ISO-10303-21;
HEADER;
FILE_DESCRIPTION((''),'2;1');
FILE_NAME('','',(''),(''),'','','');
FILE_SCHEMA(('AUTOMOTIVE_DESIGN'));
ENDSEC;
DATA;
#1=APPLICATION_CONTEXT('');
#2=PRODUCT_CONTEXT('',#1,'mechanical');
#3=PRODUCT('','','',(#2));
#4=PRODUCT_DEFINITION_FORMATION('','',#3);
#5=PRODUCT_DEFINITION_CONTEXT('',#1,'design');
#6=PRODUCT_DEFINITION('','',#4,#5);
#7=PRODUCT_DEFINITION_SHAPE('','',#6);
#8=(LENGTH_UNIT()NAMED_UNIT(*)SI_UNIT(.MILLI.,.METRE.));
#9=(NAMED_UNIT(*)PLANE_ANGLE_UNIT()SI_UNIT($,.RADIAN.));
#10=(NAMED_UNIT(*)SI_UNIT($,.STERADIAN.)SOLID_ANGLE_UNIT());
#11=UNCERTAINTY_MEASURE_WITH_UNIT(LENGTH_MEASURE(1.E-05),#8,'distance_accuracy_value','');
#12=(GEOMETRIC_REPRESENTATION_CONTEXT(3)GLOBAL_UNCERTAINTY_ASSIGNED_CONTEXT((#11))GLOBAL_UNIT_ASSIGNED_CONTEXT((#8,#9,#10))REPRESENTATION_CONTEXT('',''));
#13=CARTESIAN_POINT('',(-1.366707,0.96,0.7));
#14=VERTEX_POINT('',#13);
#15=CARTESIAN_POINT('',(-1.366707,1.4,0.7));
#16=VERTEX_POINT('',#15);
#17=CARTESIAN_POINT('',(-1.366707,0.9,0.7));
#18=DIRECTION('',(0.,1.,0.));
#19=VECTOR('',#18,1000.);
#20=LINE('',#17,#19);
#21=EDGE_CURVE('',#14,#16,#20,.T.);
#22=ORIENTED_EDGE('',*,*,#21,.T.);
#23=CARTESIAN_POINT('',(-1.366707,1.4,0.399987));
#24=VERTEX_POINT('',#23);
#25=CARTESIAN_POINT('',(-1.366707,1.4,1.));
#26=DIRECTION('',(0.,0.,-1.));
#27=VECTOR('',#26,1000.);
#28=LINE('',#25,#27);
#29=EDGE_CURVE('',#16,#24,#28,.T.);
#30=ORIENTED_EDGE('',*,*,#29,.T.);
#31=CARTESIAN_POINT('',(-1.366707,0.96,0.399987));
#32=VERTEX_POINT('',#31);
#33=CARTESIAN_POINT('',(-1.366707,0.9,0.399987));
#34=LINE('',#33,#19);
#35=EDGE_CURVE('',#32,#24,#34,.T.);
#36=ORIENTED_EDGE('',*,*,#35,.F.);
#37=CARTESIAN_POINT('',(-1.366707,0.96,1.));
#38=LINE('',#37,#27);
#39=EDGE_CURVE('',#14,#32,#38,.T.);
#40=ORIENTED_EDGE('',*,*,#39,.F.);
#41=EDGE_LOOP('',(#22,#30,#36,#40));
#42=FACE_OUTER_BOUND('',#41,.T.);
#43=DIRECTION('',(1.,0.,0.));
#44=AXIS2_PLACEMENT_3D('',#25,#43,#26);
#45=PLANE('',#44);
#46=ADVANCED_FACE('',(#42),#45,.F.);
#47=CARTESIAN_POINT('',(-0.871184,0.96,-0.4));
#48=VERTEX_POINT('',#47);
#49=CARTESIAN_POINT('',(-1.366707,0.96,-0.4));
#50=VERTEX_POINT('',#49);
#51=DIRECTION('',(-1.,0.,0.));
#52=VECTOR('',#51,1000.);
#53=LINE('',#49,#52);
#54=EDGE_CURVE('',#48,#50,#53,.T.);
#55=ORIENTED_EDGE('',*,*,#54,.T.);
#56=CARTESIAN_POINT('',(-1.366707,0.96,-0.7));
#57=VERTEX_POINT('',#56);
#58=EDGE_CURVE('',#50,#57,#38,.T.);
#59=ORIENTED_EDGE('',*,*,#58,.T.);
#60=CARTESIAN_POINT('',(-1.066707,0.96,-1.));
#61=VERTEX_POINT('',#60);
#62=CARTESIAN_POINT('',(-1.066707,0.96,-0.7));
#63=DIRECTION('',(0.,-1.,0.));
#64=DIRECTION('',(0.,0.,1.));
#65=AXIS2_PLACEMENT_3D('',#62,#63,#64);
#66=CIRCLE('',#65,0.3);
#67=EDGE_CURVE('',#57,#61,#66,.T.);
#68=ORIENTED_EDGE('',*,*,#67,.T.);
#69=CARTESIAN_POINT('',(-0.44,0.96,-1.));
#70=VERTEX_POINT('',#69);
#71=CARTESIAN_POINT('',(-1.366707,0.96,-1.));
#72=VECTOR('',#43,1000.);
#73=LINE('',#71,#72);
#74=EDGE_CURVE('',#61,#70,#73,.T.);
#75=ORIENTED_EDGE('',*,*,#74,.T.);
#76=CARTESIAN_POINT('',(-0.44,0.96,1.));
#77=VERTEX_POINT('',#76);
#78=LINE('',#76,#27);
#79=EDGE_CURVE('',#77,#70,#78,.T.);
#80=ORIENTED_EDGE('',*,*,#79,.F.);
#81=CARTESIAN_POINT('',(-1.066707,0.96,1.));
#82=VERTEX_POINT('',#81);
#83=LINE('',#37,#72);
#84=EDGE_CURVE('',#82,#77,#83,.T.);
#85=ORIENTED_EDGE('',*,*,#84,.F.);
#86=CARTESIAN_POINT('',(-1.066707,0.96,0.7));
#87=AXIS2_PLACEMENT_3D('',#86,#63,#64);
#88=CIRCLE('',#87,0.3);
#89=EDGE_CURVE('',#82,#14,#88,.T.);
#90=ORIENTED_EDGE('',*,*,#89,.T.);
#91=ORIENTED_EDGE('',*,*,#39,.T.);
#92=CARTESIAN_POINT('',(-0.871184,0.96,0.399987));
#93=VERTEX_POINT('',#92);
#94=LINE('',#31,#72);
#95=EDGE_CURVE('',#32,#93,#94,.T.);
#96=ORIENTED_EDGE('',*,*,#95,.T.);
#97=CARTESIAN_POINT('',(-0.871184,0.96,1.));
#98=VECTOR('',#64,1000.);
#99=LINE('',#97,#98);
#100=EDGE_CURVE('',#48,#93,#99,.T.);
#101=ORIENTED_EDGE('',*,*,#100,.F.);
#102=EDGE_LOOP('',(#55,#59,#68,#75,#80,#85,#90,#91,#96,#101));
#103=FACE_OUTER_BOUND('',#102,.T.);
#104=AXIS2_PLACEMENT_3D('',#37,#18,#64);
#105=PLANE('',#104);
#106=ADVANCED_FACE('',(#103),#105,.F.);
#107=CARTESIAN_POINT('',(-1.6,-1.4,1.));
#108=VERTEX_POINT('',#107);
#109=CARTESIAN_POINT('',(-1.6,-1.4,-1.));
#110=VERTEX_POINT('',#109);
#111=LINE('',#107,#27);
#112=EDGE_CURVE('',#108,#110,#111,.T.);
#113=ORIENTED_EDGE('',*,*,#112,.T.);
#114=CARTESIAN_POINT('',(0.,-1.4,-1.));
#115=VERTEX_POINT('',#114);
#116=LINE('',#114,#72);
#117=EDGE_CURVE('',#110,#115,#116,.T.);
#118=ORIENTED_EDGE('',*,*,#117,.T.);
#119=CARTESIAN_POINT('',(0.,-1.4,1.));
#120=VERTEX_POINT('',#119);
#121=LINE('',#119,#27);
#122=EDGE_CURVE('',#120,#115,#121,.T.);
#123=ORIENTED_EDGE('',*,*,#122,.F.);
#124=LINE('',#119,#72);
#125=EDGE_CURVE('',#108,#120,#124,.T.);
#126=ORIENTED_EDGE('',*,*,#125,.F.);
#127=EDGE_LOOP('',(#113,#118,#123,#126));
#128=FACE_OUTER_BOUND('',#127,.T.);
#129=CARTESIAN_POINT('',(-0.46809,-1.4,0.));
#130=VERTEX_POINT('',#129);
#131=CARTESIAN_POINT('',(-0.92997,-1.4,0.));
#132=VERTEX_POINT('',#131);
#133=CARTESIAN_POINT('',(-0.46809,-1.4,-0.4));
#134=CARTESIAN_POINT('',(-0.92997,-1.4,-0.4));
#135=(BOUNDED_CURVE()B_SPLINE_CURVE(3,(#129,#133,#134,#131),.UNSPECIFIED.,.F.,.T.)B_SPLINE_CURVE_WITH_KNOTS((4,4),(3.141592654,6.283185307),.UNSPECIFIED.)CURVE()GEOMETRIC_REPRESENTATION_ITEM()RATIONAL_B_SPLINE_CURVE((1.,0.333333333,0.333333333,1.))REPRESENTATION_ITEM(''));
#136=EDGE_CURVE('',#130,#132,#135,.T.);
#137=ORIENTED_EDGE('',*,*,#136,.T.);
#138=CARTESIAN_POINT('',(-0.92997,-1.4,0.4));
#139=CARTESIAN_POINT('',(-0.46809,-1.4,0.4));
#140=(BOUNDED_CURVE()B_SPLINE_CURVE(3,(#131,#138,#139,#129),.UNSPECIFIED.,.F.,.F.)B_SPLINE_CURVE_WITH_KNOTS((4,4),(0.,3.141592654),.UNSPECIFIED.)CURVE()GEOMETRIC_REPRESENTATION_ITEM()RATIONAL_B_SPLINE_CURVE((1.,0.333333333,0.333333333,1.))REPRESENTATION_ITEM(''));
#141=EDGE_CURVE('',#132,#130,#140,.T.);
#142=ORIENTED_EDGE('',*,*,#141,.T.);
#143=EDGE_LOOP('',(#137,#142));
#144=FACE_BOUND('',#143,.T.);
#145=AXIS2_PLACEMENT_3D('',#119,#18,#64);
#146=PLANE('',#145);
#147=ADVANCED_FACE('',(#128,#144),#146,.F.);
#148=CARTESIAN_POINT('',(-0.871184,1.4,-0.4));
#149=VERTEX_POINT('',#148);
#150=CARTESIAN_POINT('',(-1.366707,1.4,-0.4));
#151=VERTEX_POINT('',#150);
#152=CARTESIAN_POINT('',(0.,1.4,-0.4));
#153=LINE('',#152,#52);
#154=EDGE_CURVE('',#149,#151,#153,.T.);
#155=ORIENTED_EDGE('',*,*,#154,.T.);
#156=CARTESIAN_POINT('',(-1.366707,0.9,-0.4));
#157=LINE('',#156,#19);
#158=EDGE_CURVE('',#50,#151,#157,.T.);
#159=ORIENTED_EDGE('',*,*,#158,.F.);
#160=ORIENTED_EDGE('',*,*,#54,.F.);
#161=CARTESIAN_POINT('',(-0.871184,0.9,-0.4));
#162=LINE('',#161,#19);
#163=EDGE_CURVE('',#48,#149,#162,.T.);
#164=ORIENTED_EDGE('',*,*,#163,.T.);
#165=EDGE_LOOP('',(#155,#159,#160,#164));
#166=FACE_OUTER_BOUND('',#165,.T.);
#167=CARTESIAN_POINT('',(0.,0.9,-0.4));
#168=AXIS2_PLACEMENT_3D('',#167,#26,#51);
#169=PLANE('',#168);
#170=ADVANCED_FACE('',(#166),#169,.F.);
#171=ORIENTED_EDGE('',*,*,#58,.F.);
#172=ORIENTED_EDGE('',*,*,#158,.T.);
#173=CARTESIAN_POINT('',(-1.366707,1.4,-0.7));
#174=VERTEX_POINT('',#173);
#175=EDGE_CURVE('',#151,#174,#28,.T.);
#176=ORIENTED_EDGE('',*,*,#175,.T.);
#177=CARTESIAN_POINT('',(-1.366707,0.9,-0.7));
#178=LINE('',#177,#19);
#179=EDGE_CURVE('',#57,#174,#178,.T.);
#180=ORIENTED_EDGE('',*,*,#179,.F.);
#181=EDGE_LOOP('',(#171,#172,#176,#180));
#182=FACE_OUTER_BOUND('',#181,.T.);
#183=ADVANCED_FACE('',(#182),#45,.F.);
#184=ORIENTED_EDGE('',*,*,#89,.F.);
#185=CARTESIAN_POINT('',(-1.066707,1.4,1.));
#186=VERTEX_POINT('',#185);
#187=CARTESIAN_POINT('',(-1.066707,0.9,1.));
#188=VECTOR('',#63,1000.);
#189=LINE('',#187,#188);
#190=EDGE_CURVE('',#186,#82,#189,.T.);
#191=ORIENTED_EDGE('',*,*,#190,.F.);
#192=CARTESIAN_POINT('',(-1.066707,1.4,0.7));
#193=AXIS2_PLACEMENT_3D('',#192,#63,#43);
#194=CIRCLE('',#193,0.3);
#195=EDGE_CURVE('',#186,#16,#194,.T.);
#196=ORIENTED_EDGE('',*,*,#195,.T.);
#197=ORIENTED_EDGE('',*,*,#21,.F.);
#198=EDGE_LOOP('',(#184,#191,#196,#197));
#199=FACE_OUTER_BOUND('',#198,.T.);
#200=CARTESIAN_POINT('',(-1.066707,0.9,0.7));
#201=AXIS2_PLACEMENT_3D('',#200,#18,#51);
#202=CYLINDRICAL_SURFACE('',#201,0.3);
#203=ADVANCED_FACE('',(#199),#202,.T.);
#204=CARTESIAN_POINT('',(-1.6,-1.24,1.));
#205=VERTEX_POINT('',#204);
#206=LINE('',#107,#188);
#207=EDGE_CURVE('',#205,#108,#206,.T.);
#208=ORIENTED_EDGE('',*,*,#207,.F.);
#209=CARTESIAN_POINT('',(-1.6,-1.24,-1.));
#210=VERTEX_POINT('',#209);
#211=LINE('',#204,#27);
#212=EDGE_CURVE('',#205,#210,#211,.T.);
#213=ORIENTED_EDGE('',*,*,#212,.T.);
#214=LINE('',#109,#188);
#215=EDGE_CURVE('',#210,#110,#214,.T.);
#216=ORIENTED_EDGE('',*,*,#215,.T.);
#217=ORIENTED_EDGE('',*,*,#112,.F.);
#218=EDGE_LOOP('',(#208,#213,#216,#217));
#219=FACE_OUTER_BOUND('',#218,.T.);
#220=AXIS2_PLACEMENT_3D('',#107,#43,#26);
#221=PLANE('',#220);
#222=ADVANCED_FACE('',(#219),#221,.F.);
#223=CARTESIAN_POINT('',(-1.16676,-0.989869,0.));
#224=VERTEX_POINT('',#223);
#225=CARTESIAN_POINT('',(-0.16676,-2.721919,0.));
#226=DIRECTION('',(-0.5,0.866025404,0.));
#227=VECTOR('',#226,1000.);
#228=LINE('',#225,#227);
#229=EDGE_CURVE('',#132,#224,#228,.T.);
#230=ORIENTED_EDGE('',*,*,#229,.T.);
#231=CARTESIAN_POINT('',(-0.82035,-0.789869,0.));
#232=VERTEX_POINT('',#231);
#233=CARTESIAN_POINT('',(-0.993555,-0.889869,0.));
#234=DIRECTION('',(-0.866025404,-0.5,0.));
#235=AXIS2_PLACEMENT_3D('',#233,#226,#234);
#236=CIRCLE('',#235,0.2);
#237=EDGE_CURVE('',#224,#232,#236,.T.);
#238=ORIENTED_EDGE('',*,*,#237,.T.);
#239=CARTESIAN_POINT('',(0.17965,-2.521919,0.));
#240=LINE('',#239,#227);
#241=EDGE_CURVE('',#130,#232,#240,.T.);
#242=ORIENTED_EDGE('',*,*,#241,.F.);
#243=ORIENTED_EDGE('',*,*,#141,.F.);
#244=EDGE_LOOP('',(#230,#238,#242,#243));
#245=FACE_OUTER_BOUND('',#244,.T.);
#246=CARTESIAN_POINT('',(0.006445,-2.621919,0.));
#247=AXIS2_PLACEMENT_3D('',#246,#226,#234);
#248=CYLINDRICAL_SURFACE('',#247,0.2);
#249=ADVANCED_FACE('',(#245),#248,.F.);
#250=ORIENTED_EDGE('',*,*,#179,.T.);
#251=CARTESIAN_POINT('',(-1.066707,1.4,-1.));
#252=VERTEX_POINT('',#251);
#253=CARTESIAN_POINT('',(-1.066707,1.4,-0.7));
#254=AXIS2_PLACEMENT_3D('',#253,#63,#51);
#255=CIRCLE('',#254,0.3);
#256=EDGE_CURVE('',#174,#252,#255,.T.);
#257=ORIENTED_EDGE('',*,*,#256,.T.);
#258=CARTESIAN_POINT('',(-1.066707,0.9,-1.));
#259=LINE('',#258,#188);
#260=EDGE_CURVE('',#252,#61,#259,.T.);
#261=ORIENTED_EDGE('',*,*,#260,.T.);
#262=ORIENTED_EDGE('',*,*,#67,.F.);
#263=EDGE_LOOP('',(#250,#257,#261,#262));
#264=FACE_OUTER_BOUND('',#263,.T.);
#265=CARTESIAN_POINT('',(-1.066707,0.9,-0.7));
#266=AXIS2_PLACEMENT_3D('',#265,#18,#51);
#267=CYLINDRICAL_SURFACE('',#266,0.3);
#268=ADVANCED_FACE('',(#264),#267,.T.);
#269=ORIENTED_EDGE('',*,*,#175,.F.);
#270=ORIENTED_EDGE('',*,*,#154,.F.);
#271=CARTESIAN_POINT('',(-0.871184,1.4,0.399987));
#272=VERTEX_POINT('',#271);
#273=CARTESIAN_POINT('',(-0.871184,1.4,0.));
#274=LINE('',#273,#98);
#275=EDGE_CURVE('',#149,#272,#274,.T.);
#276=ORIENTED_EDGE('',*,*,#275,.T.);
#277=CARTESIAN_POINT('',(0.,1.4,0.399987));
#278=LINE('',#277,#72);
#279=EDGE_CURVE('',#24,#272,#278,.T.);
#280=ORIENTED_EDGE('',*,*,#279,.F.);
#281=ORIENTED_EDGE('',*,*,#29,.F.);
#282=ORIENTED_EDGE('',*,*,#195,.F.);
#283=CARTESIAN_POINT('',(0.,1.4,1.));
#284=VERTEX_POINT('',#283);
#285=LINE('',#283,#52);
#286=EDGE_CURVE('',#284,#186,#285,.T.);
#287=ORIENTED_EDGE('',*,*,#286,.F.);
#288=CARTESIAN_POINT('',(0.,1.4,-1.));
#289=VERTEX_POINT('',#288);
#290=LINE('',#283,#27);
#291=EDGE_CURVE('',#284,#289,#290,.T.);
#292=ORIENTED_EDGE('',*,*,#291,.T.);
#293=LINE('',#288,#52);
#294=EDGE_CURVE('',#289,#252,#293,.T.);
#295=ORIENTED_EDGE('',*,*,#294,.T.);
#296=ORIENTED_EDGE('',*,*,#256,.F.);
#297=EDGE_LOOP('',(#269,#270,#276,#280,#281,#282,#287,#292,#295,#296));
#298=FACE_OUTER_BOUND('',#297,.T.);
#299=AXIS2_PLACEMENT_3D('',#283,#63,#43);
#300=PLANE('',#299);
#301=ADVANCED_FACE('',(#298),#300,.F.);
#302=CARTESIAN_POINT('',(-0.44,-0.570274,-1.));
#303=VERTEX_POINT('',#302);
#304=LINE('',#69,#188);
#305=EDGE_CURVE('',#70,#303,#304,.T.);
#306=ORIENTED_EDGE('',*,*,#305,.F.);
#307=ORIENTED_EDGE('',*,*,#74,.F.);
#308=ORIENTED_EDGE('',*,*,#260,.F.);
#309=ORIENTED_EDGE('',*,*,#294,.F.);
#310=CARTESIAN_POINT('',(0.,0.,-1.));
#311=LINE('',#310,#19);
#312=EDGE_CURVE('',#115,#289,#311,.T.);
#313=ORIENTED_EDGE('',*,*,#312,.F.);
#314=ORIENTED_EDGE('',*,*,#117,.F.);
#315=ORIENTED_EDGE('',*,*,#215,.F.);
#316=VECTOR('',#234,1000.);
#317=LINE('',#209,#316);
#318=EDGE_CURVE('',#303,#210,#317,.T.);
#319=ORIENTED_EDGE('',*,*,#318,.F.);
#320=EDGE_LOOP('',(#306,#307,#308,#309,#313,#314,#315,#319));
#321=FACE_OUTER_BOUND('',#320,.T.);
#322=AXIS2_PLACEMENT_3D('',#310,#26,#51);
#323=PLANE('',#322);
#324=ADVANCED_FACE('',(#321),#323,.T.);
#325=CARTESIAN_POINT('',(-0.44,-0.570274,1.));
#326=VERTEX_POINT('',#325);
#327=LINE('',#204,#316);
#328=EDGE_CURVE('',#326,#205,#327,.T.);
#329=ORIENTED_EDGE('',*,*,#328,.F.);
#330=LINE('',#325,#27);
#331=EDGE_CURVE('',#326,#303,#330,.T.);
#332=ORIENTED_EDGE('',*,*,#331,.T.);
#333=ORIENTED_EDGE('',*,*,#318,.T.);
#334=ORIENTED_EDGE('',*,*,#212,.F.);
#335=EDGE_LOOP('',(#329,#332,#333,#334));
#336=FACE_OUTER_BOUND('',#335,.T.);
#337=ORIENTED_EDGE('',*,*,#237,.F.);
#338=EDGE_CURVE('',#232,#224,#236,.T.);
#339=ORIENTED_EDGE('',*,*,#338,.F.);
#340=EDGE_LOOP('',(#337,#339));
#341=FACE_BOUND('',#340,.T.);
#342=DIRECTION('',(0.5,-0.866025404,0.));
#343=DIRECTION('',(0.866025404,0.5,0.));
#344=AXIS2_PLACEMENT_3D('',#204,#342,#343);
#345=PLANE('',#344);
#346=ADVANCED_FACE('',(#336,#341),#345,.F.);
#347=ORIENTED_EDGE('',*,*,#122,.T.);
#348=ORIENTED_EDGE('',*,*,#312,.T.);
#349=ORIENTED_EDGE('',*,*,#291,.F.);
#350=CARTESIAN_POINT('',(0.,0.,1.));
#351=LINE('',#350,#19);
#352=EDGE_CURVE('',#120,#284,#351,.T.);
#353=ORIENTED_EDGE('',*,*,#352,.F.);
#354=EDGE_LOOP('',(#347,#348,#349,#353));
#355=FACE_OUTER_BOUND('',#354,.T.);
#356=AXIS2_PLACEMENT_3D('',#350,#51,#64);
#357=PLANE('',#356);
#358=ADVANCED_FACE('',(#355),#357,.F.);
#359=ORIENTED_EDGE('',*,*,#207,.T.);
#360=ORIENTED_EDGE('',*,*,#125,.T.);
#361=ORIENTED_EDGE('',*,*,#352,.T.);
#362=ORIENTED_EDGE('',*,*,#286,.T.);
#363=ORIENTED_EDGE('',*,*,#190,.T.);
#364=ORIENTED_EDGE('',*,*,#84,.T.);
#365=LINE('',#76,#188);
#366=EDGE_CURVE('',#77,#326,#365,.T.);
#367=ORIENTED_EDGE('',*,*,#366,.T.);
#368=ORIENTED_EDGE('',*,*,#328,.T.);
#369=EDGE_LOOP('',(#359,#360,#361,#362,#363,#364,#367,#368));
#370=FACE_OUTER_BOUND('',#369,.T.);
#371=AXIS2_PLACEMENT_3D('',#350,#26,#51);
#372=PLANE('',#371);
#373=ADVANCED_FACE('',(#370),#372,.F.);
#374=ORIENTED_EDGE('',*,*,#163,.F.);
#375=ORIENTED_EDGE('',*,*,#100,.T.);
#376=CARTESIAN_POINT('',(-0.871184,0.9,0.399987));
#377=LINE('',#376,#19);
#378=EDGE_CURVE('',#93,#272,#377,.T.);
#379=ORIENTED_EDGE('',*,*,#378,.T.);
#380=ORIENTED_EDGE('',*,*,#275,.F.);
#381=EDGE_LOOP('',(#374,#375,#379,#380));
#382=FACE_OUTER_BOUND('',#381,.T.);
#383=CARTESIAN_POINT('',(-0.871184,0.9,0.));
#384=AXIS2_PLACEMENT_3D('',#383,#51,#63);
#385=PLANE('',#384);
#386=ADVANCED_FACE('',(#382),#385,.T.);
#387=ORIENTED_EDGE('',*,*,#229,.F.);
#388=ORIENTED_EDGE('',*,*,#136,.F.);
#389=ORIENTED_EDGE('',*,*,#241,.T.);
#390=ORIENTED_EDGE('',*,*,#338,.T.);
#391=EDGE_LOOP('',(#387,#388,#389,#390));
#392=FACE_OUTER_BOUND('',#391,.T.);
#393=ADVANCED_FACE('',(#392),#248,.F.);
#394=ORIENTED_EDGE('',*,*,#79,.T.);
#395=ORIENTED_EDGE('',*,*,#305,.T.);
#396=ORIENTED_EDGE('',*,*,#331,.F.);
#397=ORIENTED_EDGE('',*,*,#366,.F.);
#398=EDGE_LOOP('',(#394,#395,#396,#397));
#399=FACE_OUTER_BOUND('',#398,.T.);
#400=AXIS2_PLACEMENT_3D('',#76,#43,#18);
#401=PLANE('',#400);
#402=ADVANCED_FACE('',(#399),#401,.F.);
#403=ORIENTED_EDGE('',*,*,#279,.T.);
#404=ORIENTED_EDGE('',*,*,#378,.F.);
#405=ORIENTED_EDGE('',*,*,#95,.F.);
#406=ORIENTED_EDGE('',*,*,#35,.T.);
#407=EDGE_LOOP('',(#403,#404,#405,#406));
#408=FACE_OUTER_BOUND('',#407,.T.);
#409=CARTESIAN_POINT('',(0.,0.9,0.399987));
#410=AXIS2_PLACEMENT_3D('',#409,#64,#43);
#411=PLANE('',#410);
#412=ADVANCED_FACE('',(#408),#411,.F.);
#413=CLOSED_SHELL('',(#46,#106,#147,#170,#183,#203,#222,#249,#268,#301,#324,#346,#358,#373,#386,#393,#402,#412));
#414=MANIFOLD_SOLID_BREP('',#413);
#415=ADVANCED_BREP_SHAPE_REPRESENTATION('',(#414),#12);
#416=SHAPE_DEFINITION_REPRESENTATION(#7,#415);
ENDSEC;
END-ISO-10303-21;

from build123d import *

# Parameters (mm, degrees)
BRACKET_BODY_DEPTH     = 1
CUT_0_4_SKETCH_R       = 0.2
CUT_0_4_THROUGH_DEPTH  = 2
NOTCH_0_8X0_5_SKETCH_W = 0.495523031
NOTCH_0_8X0_5_SKETCH_H = 0.799987473
NOTCH_0_8X0_5_DEPTH    = 0.5
PROFILED_NOTCH_DEPTH   = 0.5


with BuildPart() as part:
    # Bracket Profile Sketch → Bracket Body (new, symmetric)
    with BuildSketch(Plane.XY):
        Polygon((0, 0), (0, 1.4), (-1.36670697, 1.4), (-1.36670697, 0.96), (-0.44, 0.96), (-0.44, -0.570273688), (-1.6, -1.24), (-1.6, -1.4), (0, -1.4), align=None)
    extrude(amount=BRACKET_BODY_DEPTH, both=True)

    # Cut Ø0.4 Sketch → Cut Ø0.4 Through (cut)
    with BuildSketch(Plane(origin=(0.13693575, -0.237179677, 0), x_dir=(0.866025403784438, 0.5000000000000012, 0), z_dir=(-0.5000000000000012, 0.866025403784438, 0))):
        with Locations(Location((-1.30537787, 0, 0), (0, 0, 180))):
            Circle(CUT_0_4_SKETCH_R)
    extrude(amount=-CUT_0_4_THROUGH_DEPTH, mode=Mode.SUBTRACT)

    # Notch 0.8x0.5 Sketch → Notch 0.8x0.5 (cut)
    with BuildSketch(Plane(origin=(0, 1.4, 0), x_dir=(1, 0, 0), z_dir=(0, 1, 0))):
        with Locations((-1.118945454, 6.263e-06)):
            Rectangle(NOTCH_0_8X0_5_SKETCH_W, NOTCH_0_8X0_5_SKETCH_H)
    extrude(amount=-NOTCH_0_8X0_5_DEPTH, mode=Mode.SUBTRACT)

    # Profiled Notch Sketch → Profiled Notch (cut)
    with BuildSketch(Plane(origin=(0, 1.4, 0), x_dir=(1, 0, 0), z_dir=(0, 1, 0))):
        with BuildLine():
            Line((-1.36670697, 0.7), (-1.36670697, 1))
            Line((-1.36670697, 1), (-1.06670697, 1))
            ThreePointArc((-1.06670697, 1), (-1.278839005, 0.912132034), (-1.36670697, 0.7))
        make_face()
        with BuildLine():
            Line((-1.36670697, -0.7), (-1.36670697, -1))
            Line((-1.36670697, -1), (-1.06670697, -1))
            ThreePointArc((-1.06670697, -1), (-1.278839005, -0.912132034), (-1.36670697, -0.7))
        make_face()
    extrude(amount=-PROFILED_NOTCH_DEPTH, mode=Mode.SUBTRACT)


solid = part.part
